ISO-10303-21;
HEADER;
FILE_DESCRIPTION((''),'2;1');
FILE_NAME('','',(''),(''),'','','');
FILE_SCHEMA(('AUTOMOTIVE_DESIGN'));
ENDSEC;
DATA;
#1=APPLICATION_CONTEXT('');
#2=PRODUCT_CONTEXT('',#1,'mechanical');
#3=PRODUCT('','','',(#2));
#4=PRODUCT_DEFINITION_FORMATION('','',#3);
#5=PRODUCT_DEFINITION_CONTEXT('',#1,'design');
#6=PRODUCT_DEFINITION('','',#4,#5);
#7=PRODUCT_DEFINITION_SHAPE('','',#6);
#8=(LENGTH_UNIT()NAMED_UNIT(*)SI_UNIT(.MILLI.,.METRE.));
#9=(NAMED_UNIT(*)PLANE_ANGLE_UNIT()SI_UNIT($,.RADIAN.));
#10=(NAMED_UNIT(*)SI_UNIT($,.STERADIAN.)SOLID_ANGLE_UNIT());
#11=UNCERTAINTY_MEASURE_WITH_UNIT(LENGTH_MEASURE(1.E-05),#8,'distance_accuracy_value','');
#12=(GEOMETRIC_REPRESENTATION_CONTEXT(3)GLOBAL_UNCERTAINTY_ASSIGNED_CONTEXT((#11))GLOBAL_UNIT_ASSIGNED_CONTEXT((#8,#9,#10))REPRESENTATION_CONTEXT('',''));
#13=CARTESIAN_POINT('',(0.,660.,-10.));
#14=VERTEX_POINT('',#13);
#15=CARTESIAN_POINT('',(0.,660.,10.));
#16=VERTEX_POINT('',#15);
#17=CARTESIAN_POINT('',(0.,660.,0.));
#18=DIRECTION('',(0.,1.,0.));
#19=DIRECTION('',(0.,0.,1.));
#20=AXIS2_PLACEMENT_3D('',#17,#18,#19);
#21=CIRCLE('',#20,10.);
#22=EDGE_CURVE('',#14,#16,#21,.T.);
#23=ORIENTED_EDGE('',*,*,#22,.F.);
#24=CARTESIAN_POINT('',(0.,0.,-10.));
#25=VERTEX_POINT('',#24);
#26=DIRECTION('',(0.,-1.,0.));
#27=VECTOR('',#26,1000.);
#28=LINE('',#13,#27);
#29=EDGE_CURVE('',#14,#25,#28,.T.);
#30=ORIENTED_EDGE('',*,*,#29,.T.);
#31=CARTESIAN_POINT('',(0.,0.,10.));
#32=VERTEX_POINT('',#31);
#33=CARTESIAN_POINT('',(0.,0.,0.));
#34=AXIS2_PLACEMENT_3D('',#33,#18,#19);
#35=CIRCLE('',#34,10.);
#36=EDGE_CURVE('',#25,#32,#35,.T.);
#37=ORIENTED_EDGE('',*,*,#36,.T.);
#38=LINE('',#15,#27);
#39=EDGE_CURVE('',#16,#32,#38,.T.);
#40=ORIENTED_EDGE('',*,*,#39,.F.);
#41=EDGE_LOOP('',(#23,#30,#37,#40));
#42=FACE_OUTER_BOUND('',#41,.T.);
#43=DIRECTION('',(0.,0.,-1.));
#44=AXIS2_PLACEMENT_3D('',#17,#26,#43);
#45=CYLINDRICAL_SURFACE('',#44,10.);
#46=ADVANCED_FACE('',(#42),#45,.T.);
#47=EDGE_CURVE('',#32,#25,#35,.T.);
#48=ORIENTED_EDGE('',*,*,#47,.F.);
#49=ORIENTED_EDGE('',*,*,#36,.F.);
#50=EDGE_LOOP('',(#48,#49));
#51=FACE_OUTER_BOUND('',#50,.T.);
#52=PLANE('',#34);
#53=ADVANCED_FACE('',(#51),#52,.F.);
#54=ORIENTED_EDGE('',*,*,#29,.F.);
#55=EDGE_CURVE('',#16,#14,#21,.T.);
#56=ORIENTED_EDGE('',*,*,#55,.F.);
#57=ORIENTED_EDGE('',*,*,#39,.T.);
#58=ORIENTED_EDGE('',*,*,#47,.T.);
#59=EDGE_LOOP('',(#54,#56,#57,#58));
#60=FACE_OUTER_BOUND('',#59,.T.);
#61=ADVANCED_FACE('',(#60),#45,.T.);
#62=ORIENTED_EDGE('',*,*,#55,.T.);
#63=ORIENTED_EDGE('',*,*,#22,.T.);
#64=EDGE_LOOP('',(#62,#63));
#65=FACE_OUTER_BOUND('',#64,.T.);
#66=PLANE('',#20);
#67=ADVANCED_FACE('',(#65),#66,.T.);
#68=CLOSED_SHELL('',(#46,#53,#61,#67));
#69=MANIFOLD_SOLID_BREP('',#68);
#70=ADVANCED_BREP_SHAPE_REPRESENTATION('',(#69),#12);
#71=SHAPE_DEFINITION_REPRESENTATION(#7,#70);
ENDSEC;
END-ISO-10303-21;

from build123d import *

# Parameters (mm, degrees)
SKETCH1_R           = 10
BOSS_EXTRUDE1_DEPTH = 660


with BuildPart() as part:
    # Sketch1 → Boss-Extrude1 (new body)
    with BuildSketch(Plane(origin=(0, 0, 0), x_dir=(1, 0, 0), z_dir=(0, 1, 0))):
        with Locations(Location((0, 0, 0), (0, 0, 270))):
            Circle(SKETCH1_R)
    extrude(amount=BOSS_EXTRUDE1_DEPTH)


solid = part.part
